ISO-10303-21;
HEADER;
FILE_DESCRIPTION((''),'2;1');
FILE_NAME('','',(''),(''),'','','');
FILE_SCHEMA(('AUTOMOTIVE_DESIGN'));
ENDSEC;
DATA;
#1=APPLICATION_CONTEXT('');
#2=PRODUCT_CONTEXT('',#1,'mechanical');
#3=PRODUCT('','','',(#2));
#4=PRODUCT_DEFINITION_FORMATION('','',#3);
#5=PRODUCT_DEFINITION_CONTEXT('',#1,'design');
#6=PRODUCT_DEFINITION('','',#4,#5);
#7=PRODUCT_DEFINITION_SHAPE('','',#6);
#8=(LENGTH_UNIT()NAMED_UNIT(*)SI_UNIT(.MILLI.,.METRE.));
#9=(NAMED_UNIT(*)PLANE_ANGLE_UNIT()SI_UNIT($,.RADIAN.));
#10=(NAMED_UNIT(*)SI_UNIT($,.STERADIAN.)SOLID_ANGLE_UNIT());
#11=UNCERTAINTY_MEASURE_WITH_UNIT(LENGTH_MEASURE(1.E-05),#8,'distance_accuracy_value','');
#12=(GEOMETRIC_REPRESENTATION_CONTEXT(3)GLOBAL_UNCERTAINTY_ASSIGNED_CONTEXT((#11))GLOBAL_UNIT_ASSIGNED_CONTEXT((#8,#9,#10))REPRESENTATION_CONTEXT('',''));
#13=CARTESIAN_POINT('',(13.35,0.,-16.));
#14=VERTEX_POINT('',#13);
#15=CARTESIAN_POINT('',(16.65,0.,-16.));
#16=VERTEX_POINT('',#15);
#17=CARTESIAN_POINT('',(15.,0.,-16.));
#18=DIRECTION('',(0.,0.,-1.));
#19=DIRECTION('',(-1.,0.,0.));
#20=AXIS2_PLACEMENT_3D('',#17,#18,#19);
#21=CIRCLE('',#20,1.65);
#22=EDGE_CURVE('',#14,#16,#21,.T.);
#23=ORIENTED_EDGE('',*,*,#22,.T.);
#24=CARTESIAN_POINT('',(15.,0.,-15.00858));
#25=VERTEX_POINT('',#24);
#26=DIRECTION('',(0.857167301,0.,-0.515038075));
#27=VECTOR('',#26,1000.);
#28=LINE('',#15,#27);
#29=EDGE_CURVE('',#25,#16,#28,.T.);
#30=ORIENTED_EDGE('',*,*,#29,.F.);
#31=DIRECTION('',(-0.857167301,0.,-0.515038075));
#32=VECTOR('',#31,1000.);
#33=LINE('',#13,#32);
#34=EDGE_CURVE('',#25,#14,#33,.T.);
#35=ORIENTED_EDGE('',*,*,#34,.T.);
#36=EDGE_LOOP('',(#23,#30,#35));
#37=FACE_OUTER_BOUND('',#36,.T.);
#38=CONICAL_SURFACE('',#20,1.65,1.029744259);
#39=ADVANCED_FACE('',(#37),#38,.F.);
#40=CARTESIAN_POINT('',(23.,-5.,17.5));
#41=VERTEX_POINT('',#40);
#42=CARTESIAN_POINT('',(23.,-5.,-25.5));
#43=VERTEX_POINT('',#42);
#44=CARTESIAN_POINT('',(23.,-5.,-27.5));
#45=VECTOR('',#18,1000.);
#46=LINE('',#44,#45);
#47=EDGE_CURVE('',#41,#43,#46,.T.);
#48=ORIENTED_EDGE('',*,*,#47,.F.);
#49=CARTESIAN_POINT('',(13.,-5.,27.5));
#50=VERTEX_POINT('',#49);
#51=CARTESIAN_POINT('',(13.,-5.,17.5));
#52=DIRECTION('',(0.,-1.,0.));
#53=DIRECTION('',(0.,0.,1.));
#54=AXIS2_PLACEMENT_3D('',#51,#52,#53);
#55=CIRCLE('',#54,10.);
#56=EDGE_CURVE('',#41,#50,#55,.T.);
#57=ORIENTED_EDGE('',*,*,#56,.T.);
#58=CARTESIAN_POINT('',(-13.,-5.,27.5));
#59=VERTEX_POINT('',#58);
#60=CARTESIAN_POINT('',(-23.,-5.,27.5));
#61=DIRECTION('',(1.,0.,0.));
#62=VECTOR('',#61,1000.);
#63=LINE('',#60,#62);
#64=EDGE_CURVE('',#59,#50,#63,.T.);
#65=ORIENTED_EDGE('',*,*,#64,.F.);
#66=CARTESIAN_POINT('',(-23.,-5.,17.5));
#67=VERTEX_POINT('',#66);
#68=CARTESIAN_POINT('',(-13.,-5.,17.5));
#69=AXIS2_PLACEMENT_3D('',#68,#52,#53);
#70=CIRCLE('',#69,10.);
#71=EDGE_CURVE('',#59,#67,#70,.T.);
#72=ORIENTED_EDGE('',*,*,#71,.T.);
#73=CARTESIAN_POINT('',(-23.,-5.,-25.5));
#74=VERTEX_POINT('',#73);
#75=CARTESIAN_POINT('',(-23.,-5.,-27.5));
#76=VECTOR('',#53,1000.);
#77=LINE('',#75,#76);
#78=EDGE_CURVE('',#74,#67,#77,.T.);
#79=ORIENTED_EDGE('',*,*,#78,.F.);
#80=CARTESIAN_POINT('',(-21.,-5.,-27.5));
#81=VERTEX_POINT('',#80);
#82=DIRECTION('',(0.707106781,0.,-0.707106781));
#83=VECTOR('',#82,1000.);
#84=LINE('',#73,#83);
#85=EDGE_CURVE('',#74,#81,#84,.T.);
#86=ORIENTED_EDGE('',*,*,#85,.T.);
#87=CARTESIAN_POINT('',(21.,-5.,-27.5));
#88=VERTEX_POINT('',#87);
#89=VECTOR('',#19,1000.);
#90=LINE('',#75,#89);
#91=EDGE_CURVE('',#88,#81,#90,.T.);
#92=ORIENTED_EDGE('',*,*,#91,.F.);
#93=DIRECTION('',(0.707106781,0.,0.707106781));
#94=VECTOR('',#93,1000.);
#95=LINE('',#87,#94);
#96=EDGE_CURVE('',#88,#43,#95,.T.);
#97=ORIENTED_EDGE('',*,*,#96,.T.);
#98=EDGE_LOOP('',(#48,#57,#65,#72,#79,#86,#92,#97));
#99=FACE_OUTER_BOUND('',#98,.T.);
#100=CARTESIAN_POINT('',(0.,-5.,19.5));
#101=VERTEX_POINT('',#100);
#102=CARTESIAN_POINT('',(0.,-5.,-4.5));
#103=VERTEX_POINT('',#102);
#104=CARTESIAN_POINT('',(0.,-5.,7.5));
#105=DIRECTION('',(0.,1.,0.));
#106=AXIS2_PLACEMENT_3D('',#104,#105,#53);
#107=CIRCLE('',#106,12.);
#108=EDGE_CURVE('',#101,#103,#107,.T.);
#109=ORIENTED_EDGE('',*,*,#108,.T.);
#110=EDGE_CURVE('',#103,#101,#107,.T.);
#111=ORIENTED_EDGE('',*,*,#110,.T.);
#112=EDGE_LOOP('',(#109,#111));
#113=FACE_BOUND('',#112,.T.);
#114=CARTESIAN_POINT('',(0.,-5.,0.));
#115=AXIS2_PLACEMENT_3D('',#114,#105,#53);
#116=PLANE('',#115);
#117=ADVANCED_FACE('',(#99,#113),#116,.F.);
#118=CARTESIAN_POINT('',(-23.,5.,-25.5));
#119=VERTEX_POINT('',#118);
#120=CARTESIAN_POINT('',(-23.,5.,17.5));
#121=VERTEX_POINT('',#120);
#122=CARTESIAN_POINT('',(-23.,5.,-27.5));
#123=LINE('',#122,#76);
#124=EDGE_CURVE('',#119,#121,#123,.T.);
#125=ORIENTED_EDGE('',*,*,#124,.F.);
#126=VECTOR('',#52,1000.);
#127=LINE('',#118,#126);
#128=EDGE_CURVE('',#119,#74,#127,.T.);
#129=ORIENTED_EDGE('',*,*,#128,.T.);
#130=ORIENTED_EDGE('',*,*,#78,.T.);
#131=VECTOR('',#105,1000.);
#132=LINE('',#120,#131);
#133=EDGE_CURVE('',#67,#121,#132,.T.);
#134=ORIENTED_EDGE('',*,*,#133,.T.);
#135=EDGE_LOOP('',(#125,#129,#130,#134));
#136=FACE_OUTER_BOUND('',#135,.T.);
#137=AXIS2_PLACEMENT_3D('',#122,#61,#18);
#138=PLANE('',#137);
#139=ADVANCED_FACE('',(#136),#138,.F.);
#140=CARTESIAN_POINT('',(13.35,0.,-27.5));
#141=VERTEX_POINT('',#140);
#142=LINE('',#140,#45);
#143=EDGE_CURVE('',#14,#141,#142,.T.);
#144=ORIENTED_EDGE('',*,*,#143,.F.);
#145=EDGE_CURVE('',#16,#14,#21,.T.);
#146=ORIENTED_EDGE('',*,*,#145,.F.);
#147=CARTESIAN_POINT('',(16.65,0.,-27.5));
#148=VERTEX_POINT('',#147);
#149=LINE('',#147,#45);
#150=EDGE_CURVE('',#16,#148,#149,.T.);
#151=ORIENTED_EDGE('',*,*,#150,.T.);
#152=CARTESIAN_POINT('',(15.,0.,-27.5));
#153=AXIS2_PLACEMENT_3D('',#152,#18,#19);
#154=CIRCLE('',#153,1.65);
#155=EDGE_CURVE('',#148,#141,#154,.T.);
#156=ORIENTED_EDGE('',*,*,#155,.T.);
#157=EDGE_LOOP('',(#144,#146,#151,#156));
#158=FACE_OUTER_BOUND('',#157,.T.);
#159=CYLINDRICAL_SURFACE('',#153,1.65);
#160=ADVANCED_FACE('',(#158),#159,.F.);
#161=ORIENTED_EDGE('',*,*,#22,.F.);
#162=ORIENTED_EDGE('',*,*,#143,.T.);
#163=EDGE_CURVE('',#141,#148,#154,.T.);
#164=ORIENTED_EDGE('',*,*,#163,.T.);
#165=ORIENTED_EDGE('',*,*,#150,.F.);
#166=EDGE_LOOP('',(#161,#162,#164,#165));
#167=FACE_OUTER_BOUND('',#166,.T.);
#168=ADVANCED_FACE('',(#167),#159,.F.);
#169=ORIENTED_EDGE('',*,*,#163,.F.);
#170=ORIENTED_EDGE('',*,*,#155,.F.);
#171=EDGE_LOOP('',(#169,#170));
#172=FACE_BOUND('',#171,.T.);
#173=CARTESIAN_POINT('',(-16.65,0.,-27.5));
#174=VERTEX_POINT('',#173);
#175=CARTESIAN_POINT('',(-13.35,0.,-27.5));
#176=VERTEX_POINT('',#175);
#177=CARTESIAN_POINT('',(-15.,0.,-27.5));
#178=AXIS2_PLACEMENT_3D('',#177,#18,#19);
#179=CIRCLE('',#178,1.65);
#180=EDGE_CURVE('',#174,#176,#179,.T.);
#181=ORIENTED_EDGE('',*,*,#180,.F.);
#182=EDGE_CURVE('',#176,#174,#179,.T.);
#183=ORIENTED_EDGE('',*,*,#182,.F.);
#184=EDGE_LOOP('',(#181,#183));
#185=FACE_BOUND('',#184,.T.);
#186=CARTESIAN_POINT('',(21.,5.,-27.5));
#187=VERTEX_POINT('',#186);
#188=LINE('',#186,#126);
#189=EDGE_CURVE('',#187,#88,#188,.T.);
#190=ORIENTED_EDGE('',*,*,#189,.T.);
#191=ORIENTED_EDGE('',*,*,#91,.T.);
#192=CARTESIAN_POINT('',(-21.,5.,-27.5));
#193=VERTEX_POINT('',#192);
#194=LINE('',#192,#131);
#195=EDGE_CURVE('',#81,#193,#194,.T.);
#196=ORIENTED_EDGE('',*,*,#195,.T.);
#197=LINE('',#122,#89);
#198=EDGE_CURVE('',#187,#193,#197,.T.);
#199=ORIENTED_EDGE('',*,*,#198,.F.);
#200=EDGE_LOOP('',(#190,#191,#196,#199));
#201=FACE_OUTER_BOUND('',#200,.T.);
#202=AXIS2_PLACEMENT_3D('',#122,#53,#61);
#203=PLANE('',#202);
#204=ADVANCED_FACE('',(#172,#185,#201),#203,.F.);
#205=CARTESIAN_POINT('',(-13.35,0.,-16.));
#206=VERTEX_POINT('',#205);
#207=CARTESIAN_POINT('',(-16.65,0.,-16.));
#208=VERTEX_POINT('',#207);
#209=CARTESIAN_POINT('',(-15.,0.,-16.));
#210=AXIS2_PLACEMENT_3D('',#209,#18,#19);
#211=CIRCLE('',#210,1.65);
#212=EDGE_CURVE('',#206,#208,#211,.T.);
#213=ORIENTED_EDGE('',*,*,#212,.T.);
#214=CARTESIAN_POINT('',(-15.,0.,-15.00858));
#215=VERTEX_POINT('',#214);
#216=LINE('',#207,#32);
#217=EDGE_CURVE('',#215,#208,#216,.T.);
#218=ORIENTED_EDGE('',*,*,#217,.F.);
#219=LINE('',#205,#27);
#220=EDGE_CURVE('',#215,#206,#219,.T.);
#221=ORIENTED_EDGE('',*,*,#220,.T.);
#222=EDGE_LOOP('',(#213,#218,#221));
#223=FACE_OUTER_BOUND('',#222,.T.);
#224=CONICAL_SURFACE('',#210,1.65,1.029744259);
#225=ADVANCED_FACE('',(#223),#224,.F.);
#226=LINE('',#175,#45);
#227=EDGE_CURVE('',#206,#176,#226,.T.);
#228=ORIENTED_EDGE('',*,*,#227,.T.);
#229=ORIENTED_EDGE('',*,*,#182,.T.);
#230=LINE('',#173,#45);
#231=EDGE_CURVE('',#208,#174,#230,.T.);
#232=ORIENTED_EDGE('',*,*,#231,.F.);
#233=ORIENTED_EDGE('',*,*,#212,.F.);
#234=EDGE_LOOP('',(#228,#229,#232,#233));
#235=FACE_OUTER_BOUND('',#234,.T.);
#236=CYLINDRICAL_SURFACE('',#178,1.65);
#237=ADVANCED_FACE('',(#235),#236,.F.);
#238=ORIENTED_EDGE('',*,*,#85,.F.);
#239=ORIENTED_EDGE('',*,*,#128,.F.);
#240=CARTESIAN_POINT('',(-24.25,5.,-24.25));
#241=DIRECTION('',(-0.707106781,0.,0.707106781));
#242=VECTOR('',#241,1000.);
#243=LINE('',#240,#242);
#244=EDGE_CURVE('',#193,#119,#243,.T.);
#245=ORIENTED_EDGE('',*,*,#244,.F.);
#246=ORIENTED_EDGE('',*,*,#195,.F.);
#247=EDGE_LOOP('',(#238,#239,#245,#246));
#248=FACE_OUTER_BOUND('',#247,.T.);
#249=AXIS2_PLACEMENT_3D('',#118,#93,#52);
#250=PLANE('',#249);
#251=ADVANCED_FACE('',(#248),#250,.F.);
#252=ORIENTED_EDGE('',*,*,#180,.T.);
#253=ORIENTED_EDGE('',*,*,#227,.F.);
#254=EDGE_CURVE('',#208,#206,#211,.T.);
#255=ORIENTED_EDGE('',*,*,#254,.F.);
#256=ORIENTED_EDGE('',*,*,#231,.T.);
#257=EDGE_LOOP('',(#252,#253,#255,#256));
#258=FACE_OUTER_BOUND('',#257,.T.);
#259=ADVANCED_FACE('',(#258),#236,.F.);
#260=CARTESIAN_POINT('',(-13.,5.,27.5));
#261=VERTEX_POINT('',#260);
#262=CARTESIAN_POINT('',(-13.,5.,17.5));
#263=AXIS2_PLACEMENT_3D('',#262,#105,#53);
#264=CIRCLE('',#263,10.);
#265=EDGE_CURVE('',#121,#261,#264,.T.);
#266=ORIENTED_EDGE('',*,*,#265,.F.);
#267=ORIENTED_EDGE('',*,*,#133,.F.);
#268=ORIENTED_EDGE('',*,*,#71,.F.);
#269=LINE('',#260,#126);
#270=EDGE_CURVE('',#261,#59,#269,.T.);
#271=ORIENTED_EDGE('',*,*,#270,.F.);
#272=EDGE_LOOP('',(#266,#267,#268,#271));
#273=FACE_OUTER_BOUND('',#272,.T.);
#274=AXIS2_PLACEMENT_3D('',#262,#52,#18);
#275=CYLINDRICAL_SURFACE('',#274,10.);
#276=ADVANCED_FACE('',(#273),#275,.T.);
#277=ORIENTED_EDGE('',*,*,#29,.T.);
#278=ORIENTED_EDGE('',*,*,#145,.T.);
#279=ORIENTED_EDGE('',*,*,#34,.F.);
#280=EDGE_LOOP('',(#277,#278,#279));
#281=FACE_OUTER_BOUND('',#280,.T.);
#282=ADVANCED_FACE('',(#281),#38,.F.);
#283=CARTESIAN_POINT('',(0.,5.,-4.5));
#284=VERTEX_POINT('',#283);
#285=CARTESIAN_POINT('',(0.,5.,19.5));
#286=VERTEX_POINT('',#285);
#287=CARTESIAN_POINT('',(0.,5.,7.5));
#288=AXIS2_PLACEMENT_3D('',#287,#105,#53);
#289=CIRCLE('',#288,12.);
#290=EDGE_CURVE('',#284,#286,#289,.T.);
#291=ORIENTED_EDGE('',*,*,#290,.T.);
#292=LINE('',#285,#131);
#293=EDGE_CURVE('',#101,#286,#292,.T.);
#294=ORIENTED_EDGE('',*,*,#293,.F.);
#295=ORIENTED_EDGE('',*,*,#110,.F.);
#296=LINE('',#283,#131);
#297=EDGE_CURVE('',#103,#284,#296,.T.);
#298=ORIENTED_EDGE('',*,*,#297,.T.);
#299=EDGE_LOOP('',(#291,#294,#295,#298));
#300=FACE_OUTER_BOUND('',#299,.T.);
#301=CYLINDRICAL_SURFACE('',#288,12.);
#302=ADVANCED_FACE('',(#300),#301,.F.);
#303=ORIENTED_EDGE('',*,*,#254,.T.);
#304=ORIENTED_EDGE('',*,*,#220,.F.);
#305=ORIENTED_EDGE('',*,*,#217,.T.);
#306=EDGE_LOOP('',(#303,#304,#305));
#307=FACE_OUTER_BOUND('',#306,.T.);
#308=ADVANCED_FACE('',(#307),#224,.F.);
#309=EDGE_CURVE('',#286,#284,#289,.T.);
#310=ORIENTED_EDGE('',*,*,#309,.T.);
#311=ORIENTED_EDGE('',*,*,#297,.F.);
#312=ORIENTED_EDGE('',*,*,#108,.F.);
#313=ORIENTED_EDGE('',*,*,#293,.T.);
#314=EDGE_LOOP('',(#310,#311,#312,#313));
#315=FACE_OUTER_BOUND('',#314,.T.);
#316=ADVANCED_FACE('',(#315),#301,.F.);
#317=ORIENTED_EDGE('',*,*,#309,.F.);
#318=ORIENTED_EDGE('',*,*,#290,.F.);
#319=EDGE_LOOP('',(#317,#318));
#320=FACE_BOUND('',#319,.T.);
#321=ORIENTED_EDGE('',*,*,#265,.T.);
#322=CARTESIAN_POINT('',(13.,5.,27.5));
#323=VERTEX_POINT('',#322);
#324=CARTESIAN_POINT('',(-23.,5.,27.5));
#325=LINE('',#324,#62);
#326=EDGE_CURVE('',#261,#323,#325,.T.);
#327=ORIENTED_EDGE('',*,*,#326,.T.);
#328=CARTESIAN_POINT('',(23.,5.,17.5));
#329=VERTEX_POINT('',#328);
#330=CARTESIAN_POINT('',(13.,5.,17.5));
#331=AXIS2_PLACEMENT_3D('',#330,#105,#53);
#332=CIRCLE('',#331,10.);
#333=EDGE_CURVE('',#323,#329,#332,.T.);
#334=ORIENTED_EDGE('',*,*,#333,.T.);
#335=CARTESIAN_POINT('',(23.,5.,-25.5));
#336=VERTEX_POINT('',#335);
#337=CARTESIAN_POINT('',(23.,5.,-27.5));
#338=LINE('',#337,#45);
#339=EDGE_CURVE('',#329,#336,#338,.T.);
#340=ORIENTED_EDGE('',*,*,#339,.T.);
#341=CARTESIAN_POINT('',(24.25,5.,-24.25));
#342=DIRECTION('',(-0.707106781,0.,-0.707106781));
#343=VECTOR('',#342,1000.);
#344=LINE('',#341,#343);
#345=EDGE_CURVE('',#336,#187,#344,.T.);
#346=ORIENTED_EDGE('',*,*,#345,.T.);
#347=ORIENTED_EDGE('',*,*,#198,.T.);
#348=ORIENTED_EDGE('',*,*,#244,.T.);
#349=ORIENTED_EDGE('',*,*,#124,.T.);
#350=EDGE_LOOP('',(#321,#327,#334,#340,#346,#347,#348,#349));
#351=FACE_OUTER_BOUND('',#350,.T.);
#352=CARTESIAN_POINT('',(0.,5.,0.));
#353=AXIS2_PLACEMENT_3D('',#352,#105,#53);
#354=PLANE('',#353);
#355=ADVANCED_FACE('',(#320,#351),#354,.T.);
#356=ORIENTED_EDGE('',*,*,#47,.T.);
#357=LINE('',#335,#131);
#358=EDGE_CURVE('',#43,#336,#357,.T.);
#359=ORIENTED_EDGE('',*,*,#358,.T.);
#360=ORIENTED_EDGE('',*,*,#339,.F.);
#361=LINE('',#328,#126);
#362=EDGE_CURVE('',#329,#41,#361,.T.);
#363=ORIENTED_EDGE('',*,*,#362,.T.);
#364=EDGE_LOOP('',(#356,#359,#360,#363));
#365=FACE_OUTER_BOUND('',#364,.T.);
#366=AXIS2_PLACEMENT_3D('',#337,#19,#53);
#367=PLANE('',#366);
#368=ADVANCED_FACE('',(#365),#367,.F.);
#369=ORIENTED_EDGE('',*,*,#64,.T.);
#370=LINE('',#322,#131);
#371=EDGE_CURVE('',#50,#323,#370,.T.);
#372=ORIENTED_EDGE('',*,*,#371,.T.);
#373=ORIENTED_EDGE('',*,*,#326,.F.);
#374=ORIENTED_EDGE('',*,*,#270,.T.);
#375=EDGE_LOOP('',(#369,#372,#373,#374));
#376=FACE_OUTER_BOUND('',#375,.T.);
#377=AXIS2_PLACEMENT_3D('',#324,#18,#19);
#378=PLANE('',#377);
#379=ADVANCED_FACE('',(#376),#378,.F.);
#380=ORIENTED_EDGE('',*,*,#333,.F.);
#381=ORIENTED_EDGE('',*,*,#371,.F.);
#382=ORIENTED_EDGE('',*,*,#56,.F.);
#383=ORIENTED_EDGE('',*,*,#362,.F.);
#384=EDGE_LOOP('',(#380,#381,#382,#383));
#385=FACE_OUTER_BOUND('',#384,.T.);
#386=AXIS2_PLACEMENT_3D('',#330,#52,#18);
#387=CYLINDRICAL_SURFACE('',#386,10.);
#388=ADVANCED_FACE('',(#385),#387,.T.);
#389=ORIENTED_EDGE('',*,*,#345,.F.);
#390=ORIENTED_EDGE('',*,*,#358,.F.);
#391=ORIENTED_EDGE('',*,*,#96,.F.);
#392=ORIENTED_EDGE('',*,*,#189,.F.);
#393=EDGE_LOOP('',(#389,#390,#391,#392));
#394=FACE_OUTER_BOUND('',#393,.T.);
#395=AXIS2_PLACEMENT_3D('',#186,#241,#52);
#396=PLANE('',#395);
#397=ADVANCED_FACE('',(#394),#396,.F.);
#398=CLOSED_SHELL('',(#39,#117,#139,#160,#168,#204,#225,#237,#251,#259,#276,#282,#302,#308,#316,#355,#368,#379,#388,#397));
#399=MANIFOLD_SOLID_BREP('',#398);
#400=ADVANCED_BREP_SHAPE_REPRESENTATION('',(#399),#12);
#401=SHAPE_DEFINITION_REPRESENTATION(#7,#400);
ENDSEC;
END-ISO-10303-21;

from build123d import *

# Parameters (mm, degrees)
SKETCH_1_W             = 46
SKETCH_1_H             = 55
EXTRUDE_1_DEPTH        = 5
HOLE_WIZARD_M27_1_0_D  = 24
FILLET_1_R             = 10
HOLE_WIZARD_M4_1_D     = 3.3
HOLE_WIZARD_M4_1_DEPTH = 11.5
HOLE_WIZARD_M4_1_TIP   = 0.991420021
CHAMFER_1_SIZE         = 2


with BuildPart() as part:
    # 草图1 → 凸台-拉伸1 (new, symmetric)
    with BuildSketch(Plane(origin=(0, 0, 0), x_dir=(1, 0, 0), z_dir=(0, 1, 0))):
        Rectangle(SKETCH_1_W, SKETCH_1_H)
    extrude(amount=EXTRUDE_1_DEPTH, both=True)

    # M27*1.0反牙 (through all)
    with Locations(Plane(origin=(0, 5, 0), x_dir=(1, 0, 0), z_dir=(0, 1, 0))):
        with Locations((0, -7.5)):
            Hole(HOLE_WIZARD_M27_1_0_D / 2)

    # 圆角1
    fillet_1_edges = [part.edges().sort_by_distance(p)[0] for p in [
        (23, 0, 27.5),
        (-23, 0, 27.5),
    ]]
    fillet(fillet_1_edges, radius=FILLET_1_R)

    # M4 螺纹孔1
    with Locations(Plane(origin=(0, 0, -27.5), x_dir=(-1, 0, 0), z_dir=(0, 0, -1))):
        with Locations((-15, 0), (15, 0)):
            Hole(HOLE_WIZARD_M4_1_D / 2, depth=HOLE_WIZARD_M4_1_DEPTH)
            with Locations((0, 0, -(HOLE_WIZARD_M4_1_DEPTH + HOLE_WIZARD_M4_1_TIP / 2))):  # 118° drill point
                Cone(0, HOLE_WIZARD_M4_1_D / 2, HOLE_WIZARD_M4_1_TIP, mode=Mode.SUBTRACT)

    # 倒角1
    chamfer_1_edges = [part.edges().sort_by_distance(p)[0] for p in [
        (-23, 0, -27.5),
        (23, 0, -27.5),
    ]]
    chamfer(chamfer_1_edges, length=CHAMFER_1_SIZE)


solid = part.part
